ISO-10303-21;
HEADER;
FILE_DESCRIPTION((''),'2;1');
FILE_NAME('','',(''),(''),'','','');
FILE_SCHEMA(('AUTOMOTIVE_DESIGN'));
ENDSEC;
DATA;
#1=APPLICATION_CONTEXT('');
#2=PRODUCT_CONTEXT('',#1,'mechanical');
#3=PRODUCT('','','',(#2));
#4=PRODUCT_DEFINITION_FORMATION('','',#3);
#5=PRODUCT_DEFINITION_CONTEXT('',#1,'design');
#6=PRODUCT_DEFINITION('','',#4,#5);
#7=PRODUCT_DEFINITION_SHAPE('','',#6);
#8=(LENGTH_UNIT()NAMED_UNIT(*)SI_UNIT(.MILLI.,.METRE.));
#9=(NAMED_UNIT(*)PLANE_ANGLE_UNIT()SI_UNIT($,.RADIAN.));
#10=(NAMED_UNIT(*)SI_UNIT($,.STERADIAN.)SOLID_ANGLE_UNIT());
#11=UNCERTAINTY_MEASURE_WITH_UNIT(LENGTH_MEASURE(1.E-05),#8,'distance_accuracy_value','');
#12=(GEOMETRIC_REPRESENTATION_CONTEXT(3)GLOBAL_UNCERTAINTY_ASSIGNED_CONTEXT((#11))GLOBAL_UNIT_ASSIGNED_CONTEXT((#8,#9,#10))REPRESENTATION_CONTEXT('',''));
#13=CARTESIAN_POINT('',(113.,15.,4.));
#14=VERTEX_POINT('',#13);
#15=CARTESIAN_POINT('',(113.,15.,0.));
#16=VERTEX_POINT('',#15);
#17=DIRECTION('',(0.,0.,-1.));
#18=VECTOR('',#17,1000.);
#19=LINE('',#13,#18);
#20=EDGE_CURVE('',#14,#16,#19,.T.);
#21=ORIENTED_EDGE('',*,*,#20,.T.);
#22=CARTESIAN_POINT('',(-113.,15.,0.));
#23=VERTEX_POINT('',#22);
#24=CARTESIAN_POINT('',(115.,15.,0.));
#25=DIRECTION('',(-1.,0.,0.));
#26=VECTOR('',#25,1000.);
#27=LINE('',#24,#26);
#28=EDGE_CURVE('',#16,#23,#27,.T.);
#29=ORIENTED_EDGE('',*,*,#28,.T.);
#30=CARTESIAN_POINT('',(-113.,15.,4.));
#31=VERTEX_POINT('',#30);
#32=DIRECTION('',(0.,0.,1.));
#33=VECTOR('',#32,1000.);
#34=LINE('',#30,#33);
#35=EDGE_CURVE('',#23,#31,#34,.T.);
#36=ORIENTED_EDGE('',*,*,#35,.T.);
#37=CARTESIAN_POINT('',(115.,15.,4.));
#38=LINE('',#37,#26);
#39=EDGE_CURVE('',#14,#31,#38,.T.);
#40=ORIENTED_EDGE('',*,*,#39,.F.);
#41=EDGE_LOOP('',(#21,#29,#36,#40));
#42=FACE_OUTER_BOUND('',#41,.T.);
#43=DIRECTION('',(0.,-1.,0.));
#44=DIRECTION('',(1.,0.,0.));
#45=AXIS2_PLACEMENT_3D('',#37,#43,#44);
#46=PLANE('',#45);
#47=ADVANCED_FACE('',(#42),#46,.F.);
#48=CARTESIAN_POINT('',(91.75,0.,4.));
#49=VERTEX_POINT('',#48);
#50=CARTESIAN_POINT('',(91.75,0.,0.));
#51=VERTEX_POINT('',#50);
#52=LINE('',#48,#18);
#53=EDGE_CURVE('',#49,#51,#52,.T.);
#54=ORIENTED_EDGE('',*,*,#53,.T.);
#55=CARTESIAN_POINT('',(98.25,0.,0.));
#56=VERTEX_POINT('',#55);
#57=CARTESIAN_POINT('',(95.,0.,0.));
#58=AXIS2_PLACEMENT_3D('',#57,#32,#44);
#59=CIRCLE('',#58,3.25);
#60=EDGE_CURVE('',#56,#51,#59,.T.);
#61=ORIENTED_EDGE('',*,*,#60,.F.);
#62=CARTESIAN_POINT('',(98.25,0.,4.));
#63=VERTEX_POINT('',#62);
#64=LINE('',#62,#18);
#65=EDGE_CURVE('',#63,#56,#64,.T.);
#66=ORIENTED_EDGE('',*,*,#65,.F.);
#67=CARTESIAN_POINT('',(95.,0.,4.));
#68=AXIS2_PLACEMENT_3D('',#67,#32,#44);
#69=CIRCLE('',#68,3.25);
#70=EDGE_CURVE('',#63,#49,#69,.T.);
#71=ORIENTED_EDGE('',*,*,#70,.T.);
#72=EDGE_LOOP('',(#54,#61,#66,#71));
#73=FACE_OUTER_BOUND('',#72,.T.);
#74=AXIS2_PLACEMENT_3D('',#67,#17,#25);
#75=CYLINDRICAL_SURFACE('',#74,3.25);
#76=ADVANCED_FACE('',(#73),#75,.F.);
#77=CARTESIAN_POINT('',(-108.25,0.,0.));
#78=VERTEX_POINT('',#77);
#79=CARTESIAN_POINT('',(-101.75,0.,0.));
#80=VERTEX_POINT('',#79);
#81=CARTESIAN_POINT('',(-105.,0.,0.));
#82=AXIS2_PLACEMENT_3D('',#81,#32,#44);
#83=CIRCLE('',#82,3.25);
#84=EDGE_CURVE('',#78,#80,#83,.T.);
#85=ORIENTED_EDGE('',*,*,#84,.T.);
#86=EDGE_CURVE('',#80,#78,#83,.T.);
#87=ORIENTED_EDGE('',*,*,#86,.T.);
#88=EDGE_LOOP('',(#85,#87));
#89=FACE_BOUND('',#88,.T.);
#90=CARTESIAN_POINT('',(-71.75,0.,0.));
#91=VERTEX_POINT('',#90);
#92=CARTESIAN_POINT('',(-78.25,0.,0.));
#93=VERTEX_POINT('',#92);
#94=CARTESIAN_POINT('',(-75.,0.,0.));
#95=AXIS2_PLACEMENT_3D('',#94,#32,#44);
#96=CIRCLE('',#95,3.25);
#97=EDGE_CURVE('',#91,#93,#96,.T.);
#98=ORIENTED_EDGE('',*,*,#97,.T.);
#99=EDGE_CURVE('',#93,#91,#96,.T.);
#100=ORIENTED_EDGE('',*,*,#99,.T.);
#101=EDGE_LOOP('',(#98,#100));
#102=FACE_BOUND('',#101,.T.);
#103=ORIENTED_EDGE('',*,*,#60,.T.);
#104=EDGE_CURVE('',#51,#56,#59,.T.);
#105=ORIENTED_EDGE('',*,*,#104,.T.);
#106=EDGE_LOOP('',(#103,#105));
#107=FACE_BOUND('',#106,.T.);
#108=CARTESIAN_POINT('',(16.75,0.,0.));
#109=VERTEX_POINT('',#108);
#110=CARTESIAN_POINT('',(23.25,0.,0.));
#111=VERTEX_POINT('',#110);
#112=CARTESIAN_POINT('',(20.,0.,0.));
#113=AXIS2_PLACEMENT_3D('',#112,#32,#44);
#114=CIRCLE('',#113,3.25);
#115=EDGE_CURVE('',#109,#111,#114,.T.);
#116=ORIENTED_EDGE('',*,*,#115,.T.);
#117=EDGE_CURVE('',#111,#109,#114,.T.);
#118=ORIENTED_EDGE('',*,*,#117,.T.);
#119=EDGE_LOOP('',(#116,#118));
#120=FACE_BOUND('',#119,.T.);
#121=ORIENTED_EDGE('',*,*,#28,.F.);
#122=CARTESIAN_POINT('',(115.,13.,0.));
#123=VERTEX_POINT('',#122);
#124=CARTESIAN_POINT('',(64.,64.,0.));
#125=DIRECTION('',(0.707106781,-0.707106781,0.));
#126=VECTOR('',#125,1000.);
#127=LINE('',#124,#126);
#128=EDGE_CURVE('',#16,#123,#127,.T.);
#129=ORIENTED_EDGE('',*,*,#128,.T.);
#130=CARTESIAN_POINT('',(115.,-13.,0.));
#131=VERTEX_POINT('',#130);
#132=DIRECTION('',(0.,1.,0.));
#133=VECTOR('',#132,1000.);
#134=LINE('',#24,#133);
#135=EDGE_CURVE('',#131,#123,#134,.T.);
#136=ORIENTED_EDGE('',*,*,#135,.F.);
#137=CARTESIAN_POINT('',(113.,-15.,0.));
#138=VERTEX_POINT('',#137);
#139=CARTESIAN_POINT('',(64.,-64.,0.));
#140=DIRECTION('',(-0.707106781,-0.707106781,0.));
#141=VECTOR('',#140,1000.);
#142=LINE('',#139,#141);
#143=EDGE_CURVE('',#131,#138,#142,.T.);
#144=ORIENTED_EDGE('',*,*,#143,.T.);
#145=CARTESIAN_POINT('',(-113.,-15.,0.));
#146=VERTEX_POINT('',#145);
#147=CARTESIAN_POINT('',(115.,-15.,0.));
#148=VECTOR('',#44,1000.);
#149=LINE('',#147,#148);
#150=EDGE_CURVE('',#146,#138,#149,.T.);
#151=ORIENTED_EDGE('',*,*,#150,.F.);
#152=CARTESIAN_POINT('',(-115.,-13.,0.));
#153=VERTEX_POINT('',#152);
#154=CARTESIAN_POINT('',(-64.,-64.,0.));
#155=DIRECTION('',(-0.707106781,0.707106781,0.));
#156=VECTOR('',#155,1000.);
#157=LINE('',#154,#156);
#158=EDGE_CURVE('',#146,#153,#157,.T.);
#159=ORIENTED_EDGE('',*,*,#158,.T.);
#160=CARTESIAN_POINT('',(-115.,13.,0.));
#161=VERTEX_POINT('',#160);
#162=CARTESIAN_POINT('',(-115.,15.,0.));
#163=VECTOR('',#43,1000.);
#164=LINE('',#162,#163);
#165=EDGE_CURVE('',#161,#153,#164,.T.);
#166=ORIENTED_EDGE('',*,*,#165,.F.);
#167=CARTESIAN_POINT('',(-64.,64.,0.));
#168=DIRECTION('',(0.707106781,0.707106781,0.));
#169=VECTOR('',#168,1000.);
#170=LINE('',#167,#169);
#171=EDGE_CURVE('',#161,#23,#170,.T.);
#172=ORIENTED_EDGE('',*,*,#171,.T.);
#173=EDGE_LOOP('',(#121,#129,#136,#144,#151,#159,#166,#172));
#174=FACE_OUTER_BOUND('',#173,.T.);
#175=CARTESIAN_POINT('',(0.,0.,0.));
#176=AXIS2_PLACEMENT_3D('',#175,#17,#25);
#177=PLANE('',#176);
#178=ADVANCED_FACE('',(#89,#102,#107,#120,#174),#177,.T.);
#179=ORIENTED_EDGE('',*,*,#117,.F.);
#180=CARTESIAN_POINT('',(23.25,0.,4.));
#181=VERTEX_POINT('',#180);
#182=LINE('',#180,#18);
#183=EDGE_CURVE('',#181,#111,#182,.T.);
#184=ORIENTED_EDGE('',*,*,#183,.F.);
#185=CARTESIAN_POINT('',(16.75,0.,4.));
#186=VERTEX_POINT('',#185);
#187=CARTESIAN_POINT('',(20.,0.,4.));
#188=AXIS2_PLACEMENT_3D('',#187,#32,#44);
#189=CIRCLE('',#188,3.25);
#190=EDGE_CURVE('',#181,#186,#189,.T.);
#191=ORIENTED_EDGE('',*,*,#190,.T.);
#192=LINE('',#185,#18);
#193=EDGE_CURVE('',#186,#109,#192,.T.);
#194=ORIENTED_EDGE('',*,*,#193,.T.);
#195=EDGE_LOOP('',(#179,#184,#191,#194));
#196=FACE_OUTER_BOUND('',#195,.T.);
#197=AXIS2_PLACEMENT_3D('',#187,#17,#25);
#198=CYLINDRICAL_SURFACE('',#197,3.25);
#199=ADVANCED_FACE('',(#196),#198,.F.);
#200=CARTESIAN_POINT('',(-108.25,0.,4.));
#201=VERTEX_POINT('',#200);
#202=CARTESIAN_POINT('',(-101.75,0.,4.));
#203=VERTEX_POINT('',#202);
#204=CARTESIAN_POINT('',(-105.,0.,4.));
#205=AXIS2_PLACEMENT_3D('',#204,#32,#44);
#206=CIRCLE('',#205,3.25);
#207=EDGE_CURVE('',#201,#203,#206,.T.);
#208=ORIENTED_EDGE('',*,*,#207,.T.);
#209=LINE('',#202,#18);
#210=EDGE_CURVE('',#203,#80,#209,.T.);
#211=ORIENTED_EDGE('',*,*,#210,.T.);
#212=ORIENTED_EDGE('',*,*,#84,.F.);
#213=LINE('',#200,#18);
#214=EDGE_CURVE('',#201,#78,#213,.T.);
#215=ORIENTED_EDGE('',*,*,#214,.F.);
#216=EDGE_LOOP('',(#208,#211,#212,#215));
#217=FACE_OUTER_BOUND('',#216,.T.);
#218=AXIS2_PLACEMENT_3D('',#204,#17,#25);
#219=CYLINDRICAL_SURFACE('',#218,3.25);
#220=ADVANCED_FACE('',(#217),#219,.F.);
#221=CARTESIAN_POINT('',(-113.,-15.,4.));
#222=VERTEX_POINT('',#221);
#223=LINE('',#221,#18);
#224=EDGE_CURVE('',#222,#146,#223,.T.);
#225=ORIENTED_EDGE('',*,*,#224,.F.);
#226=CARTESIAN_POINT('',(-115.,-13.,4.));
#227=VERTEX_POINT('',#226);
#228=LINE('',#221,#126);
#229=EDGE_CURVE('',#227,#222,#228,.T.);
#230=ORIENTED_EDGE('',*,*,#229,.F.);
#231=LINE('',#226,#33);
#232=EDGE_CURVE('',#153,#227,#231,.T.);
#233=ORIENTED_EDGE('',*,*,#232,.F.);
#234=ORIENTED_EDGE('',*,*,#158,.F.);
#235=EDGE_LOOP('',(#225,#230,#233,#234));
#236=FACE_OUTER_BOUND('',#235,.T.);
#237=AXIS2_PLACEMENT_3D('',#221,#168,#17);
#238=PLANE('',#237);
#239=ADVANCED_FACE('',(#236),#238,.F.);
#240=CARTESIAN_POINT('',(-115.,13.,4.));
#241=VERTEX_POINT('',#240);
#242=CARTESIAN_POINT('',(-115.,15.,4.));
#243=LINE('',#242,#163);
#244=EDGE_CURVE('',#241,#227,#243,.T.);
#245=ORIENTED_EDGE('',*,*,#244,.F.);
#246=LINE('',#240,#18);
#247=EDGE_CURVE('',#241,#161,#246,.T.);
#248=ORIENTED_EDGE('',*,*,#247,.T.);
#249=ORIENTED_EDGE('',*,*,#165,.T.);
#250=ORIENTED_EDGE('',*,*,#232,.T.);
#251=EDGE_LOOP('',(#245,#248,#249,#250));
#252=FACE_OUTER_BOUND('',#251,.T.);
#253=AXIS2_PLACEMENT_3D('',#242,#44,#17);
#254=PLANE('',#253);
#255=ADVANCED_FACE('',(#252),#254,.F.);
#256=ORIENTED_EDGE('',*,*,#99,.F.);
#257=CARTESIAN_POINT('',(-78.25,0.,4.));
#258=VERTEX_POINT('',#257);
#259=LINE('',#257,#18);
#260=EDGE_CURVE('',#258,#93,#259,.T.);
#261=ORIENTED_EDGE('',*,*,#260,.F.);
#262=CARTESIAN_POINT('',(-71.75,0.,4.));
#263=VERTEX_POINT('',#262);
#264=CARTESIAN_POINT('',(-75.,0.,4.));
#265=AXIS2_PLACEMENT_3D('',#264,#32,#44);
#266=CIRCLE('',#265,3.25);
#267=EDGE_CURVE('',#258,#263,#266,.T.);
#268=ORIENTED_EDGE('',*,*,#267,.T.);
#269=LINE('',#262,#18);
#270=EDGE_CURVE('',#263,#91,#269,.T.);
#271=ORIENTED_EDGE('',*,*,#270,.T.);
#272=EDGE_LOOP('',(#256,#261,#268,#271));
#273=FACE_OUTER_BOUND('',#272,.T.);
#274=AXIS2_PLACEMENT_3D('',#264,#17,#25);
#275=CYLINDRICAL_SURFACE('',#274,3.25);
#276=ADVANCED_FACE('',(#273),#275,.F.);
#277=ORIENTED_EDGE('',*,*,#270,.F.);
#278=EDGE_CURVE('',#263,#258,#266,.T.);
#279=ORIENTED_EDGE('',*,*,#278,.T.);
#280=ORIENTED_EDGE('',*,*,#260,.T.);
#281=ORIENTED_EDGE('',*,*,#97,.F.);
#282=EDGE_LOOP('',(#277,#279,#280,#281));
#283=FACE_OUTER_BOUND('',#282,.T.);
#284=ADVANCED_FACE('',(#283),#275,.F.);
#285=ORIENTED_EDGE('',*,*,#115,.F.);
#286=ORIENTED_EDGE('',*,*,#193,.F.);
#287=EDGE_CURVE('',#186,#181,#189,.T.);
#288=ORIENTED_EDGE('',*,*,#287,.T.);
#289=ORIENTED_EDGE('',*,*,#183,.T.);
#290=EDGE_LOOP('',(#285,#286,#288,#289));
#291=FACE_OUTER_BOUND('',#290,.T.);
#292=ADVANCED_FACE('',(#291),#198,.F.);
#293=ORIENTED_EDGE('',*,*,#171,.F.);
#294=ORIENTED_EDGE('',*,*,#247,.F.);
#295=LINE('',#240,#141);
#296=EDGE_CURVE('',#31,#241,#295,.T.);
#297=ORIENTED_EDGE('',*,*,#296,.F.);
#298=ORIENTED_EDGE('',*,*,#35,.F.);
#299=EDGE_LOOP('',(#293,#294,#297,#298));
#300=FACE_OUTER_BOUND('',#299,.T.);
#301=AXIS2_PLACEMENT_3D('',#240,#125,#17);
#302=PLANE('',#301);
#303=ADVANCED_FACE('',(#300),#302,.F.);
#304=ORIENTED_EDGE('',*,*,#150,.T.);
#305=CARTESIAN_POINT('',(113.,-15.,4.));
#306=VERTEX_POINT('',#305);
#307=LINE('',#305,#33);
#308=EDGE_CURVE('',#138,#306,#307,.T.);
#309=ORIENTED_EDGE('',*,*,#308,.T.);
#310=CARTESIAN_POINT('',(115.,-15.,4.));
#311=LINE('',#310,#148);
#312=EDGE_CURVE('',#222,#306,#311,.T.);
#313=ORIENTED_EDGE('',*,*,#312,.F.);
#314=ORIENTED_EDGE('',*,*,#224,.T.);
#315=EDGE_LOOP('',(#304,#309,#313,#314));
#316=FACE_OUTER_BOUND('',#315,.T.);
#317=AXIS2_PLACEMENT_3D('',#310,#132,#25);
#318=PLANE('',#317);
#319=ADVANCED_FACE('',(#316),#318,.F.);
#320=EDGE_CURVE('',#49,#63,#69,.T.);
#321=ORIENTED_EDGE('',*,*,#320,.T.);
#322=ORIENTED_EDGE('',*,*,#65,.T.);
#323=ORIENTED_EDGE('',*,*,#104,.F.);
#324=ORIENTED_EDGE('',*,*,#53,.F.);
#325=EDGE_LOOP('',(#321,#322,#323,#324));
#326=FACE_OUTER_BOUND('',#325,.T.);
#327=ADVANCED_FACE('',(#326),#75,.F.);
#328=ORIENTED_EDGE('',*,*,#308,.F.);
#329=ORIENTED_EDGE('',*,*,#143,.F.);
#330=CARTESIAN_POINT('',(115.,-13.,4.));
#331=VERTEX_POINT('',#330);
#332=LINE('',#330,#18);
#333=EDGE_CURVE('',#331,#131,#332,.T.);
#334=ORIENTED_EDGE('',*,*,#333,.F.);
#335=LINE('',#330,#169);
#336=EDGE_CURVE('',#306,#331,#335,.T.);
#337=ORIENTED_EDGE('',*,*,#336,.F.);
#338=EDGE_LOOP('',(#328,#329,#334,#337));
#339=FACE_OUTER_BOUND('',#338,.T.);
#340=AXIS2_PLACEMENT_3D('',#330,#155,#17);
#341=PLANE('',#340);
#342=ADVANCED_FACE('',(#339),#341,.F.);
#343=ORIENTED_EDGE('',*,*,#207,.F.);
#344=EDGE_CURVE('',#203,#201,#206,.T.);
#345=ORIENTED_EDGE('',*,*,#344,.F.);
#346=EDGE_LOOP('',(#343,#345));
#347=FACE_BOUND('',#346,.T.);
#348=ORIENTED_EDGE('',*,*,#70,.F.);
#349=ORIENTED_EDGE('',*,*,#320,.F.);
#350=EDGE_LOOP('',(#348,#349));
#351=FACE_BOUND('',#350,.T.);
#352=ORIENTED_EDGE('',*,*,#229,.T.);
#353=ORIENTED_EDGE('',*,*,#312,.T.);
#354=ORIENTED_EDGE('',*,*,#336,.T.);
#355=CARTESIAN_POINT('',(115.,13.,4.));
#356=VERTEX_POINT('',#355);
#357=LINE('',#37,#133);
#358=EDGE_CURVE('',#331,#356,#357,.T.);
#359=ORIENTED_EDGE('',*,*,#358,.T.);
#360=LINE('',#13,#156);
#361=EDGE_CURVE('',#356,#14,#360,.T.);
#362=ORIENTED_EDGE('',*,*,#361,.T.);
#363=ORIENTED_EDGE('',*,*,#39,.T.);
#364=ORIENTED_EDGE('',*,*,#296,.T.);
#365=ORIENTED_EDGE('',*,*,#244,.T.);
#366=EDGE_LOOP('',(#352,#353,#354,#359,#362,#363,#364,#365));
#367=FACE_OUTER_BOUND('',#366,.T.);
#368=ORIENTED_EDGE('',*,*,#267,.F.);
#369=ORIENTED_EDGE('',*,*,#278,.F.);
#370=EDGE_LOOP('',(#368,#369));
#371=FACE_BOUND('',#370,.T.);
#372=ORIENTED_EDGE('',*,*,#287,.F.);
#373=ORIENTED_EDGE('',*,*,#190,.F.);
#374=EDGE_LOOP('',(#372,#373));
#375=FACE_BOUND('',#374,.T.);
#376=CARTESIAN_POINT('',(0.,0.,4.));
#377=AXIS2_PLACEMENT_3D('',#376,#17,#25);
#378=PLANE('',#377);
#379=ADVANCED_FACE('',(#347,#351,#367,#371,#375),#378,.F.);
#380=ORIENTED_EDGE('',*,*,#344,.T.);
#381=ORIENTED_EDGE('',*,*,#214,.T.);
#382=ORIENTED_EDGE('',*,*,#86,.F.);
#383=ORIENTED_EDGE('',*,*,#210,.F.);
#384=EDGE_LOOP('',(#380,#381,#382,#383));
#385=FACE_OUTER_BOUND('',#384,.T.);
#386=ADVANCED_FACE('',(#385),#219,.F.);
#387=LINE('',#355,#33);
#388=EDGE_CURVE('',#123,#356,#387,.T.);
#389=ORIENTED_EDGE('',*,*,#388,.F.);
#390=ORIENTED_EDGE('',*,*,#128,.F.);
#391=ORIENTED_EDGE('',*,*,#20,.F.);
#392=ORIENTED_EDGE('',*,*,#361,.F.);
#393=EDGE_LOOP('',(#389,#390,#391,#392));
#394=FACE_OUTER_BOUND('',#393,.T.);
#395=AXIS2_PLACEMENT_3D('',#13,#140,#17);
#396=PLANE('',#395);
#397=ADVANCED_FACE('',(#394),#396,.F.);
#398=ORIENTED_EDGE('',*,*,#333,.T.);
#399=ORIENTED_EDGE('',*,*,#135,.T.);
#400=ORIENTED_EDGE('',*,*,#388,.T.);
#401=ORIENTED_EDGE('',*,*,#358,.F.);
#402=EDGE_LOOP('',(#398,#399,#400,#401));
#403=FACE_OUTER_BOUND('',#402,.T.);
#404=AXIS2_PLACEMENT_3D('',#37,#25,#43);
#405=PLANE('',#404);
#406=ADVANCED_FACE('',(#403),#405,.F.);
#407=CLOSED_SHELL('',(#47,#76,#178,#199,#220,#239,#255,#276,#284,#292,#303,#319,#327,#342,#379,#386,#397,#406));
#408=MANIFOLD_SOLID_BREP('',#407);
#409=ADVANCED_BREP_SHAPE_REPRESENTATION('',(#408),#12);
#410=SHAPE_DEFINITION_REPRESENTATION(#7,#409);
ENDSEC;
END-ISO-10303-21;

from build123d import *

# Parameters (mm, degrees)
SKETCH1_W           = 230
SKETCH1_H           = 30
SKETCH1_R           = 3.25
BOSS_EXTRUDE1_DEPTH = 4
CHAMFER1_SIZE       = 2


with BuildPart() as part:
    # Sketch1 → Boss-Extrude1 (new body)
    with BuildSketch(Plane.XY):
        Rectangle(SKETCH1_W, SKETCH1_H)
        with Locations((-105, 0)):
            Circle(SKETCH1_R, mode=Mode.SUBTRACT)
        with Locations((-75, 0)):
            Circle(SKETCH1_R, mode=Mode.SUBTRACT)
        with Locations((20, 0)):
            Circle(SKETCH1_R, mode=Mode.SUBTRACT)
        with Locations((95, 0)):
            Circle(SKETCH1_R, mode=Mode.SUBTRACT)
    extrude(amount=BOSS_EXTRUDE1_DEPTH)

    # Chamfer1
    chamfer1_edges = [part.edges().sort_by_distance(p)[0] for p in [
        (-115, 15, 2),
        (115, 15, 2),
        (115, -15, 2),
        (-115, -15, 2),
    ]]
    chamfer(chamfer1_edges, length=CHAMFER1_SIZE)


solid = part.part
